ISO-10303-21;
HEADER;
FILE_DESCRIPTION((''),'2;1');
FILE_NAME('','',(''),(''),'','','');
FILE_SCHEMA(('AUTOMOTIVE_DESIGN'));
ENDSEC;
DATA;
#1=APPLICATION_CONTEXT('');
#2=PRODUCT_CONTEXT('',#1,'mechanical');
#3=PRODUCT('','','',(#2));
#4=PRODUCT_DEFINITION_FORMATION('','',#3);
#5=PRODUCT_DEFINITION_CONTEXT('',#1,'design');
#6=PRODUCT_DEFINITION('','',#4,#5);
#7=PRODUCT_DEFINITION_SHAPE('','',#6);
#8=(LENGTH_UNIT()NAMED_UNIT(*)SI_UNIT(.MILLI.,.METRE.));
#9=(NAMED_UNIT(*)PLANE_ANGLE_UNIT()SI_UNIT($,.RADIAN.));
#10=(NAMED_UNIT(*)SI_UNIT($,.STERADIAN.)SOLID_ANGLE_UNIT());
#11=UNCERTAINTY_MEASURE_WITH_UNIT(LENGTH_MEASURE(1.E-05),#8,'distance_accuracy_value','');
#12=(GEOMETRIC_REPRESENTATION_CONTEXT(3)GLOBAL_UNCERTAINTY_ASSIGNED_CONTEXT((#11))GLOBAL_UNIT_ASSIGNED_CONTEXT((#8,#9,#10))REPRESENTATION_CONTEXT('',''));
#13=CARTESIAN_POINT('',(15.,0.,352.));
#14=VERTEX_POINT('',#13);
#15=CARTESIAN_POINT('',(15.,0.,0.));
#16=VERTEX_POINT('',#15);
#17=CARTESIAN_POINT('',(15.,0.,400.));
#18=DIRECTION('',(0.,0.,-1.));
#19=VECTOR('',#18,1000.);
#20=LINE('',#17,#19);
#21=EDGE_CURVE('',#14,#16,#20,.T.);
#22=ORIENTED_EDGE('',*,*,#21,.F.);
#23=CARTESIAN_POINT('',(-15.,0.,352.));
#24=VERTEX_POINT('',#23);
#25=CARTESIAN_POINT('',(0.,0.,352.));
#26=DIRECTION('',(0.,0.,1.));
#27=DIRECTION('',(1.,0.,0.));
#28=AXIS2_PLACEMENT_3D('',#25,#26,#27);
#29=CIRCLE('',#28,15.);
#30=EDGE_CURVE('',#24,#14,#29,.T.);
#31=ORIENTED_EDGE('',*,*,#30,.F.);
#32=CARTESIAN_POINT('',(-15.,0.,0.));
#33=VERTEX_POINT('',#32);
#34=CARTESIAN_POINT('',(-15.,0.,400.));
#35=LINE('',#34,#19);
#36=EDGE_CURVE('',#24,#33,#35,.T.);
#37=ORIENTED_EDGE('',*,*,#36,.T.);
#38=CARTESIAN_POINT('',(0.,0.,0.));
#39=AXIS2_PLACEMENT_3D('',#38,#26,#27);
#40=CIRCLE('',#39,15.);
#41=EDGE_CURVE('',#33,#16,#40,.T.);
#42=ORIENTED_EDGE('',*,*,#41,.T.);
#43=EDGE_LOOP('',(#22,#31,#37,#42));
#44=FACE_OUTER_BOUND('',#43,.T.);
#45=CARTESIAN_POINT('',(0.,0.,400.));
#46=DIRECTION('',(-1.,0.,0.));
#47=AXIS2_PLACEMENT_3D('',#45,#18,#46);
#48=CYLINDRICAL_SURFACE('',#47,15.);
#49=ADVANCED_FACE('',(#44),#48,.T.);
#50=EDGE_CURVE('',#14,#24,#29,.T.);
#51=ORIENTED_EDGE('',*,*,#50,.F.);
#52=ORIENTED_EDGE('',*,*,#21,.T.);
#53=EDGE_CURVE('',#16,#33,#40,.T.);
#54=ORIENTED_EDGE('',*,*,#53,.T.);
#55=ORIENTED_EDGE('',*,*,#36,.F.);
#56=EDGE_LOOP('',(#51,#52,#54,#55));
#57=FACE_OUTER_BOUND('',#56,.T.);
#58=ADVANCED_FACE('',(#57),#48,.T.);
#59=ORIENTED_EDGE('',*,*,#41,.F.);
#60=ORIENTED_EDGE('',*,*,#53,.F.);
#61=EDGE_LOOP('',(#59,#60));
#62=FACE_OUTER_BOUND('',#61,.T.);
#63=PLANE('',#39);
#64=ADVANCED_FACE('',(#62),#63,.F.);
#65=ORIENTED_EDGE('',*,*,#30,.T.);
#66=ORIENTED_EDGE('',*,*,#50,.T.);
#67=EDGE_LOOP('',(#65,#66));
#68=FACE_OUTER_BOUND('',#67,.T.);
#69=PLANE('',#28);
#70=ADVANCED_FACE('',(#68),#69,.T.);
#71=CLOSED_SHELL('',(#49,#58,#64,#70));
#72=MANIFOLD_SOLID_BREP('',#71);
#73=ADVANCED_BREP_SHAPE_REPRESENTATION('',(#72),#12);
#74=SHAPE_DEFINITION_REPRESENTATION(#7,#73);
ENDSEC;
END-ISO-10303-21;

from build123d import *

# Parameters (mm, degrees)
SKETCH_1_R          = 15
EXTRUDE_1_DEPTH     = 400
CUT_EXTRUDE_START   = -48
SKETCH_2_R          = 15
CUT_EXTRUDE_1_DEPTH = 48


with BuildPart() as part:
    # 草图1 → 凸台-拉伸1 (new body)
    with BuildSketch(Plane.XY):
        Circle(SKETCH_1_R)
    extrude(amount=EXTRUDE_1_DEPTH)

    # 草图2 → 切除-拉伸1 (cut)
    with BuildSketch(Plane.XY.offset(400).offset(CUT_EXTRUDE_START)):
        Circle(SKETCH_2_R)
    extrude(amount=CUT_EXTRUDE_1_DEPTH, mode=Mode.SUBTRACT)


solid = part.part
